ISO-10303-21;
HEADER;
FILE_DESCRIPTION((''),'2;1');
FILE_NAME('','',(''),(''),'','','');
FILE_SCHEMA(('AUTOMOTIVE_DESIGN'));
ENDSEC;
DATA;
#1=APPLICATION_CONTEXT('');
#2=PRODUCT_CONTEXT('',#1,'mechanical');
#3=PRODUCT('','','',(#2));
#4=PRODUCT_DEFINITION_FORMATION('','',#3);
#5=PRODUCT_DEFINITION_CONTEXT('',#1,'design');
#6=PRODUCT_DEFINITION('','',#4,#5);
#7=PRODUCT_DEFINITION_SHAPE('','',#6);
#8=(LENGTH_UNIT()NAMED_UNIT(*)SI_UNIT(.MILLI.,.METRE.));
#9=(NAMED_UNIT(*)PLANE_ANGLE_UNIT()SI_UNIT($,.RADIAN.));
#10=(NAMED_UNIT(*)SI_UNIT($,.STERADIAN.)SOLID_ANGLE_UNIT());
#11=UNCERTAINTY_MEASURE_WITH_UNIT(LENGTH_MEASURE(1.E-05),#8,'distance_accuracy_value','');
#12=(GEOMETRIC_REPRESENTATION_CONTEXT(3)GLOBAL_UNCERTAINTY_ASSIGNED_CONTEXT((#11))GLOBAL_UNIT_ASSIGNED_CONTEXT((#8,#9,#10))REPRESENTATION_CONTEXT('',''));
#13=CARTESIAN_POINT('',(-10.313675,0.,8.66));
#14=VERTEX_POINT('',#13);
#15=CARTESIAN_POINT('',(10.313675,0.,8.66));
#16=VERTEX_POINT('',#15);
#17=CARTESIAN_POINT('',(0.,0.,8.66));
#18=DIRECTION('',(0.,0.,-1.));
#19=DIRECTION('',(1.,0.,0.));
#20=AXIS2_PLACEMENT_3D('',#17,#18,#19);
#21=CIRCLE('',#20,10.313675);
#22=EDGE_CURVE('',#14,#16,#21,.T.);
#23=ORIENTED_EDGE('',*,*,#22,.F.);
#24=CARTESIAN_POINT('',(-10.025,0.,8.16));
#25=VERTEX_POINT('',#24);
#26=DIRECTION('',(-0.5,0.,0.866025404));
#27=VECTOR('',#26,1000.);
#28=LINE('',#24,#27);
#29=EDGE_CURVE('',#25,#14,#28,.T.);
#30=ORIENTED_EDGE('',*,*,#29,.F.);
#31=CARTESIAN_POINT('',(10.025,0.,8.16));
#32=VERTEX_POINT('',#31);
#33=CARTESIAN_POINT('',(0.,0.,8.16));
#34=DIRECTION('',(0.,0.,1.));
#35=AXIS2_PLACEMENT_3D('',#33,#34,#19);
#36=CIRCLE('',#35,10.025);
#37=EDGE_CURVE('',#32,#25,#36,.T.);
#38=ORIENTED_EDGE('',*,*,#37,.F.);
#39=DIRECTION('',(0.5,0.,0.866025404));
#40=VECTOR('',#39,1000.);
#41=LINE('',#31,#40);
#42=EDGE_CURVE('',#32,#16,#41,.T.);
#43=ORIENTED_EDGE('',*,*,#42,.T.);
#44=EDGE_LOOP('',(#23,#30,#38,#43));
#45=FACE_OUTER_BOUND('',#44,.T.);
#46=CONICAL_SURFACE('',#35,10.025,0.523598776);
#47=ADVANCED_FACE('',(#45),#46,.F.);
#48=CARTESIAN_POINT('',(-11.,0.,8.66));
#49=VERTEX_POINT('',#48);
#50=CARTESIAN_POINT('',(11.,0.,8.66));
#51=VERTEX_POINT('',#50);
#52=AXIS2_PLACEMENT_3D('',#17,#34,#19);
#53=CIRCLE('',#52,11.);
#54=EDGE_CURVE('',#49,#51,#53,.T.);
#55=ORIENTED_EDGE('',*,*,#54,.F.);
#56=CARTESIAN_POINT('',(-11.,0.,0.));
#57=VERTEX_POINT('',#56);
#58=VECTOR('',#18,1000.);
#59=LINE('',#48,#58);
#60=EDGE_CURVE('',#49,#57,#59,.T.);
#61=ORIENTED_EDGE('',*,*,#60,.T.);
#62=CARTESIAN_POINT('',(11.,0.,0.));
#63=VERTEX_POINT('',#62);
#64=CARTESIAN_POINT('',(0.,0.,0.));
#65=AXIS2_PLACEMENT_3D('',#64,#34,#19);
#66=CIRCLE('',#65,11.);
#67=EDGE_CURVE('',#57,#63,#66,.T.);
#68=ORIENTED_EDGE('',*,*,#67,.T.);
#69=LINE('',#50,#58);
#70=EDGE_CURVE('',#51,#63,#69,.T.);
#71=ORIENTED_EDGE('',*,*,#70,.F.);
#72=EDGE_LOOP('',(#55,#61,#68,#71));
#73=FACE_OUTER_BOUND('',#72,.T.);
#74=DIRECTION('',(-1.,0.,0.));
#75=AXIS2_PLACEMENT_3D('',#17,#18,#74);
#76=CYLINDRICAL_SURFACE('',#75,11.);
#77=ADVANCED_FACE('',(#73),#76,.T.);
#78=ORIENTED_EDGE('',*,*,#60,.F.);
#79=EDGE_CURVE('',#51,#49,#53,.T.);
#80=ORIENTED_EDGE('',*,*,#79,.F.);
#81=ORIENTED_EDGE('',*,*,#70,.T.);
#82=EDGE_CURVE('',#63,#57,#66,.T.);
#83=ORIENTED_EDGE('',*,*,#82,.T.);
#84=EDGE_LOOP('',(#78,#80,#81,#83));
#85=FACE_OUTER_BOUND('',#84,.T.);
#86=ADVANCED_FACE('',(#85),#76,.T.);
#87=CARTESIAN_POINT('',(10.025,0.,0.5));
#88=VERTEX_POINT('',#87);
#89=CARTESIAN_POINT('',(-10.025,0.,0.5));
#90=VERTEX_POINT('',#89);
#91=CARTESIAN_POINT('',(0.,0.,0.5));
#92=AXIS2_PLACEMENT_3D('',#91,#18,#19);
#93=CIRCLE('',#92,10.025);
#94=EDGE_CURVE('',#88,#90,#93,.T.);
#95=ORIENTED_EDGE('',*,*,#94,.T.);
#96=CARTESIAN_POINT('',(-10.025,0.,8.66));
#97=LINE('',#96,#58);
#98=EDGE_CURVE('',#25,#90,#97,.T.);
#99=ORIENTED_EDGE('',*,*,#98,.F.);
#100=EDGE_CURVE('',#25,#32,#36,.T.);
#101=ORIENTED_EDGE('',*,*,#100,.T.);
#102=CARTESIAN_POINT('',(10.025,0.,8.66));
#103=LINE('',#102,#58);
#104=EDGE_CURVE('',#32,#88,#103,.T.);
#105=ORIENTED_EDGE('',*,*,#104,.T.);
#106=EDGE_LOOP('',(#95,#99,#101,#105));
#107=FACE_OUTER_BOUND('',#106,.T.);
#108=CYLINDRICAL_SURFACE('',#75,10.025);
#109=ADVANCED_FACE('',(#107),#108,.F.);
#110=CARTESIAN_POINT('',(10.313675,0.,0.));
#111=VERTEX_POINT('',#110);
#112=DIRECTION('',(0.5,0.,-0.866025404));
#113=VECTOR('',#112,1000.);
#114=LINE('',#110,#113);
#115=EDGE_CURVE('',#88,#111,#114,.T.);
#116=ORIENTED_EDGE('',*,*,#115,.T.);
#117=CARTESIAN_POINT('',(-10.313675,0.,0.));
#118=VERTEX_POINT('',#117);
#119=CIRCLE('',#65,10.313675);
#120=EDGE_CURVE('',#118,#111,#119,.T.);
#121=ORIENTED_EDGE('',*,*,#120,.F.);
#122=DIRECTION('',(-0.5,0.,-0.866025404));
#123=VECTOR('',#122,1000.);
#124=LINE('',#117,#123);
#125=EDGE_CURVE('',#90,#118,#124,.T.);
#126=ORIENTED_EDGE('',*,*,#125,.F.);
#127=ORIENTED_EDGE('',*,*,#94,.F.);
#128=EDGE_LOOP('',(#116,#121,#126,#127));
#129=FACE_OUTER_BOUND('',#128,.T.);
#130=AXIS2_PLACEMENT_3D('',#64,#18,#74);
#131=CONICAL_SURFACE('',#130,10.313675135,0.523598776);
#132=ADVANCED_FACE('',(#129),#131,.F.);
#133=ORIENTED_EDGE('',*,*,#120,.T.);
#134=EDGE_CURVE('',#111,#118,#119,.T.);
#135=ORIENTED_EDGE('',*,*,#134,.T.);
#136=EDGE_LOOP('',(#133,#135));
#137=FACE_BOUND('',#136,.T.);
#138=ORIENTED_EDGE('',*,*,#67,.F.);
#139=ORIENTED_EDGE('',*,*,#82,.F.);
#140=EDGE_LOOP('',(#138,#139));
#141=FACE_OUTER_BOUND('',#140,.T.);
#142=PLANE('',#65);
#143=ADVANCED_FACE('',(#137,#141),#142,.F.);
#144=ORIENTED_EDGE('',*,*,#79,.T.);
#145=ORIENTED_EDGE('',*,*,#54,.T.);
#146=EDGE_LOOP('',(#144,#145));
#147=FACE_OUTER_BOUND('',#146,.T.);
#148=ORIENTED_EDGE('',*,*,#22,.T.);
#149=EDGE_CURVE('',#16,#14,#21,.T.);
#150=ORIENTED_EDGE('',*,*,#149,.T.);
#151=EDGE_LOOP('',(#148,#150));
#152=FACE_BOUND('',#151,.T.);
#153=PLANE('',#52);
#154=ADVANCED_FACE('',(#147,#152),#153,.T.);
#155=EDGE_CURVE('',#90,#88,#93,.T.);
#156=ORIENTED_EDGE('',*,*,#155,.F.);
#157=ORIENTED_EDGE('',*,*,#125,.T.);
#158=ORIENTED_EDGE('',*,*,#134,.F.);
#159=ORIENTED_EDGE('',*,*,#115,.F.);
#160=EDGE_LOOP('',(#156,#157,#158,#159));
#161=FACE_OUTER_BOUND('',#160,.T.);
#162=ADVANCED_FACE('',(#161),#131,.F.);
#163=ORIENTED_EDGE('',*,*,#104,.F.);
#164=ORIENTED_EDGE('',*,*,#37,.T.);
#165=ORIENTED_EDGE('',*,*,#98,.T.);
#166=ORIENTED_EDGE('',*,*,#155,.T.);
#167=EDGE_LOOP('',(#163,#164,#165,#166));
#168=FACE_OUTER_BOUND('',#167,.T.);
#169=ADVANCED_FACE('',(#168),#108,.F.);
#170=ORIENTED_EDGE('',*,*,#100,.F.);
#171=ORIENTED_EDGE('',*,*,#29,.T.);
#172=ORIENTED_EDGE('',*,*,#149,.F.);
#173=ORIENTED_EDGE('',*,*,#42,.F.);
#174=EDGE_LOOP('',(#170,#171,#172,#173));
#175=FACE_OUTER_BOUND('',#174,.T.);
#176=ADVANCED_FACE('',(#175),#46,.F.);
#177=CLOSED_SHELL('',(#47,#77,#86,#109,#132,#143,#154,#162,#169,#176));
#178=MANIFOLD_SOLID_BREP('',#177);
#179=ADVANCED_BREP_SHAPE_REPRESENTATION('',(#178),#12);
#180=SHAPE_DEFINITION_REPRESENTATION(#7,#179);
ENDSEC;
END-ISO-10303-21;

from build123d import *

# Parameters (mm, degrees)
SKETCH_1_R      = 11
SKETCH_1_R_2    = 10.025
EXTRUDE_1_DEPTH = 8.66
CHAMFER_1_SIZE  = 0.5
CHAMFER_1_SIZE2 = 0.288675135


with BuildPart() as part:
    # 草图1 → 凸台-拉伸1 (new body)
    with BuildSketch(Plane.XY):
        Circle(SKETCH_1_R)
        Circle(SKETCH_1_R_2, mode=Mode.SUBTRACT)
    extrude(amount=EXTRUDE_1_DEPTH)

    # 倒角1
    chamfer_1_edges = [part.edges().sort_by_distance(p)[0] for p in [
        (-10.025, 0, 0),
        (-10.025, 0, 8.66),
    ]]
    chamfer_1_side = [part.faces().sort_by_distance(p)[0] for p in [
        (-10.025, 0, 4.33),
    ]]
    chamfer(chamfer_1_edges, length=CHAMFER_1_SIZE, length2=CHAMFER_1_SIZE2, reference=chamfer_1_side[0])


solid = part.part
